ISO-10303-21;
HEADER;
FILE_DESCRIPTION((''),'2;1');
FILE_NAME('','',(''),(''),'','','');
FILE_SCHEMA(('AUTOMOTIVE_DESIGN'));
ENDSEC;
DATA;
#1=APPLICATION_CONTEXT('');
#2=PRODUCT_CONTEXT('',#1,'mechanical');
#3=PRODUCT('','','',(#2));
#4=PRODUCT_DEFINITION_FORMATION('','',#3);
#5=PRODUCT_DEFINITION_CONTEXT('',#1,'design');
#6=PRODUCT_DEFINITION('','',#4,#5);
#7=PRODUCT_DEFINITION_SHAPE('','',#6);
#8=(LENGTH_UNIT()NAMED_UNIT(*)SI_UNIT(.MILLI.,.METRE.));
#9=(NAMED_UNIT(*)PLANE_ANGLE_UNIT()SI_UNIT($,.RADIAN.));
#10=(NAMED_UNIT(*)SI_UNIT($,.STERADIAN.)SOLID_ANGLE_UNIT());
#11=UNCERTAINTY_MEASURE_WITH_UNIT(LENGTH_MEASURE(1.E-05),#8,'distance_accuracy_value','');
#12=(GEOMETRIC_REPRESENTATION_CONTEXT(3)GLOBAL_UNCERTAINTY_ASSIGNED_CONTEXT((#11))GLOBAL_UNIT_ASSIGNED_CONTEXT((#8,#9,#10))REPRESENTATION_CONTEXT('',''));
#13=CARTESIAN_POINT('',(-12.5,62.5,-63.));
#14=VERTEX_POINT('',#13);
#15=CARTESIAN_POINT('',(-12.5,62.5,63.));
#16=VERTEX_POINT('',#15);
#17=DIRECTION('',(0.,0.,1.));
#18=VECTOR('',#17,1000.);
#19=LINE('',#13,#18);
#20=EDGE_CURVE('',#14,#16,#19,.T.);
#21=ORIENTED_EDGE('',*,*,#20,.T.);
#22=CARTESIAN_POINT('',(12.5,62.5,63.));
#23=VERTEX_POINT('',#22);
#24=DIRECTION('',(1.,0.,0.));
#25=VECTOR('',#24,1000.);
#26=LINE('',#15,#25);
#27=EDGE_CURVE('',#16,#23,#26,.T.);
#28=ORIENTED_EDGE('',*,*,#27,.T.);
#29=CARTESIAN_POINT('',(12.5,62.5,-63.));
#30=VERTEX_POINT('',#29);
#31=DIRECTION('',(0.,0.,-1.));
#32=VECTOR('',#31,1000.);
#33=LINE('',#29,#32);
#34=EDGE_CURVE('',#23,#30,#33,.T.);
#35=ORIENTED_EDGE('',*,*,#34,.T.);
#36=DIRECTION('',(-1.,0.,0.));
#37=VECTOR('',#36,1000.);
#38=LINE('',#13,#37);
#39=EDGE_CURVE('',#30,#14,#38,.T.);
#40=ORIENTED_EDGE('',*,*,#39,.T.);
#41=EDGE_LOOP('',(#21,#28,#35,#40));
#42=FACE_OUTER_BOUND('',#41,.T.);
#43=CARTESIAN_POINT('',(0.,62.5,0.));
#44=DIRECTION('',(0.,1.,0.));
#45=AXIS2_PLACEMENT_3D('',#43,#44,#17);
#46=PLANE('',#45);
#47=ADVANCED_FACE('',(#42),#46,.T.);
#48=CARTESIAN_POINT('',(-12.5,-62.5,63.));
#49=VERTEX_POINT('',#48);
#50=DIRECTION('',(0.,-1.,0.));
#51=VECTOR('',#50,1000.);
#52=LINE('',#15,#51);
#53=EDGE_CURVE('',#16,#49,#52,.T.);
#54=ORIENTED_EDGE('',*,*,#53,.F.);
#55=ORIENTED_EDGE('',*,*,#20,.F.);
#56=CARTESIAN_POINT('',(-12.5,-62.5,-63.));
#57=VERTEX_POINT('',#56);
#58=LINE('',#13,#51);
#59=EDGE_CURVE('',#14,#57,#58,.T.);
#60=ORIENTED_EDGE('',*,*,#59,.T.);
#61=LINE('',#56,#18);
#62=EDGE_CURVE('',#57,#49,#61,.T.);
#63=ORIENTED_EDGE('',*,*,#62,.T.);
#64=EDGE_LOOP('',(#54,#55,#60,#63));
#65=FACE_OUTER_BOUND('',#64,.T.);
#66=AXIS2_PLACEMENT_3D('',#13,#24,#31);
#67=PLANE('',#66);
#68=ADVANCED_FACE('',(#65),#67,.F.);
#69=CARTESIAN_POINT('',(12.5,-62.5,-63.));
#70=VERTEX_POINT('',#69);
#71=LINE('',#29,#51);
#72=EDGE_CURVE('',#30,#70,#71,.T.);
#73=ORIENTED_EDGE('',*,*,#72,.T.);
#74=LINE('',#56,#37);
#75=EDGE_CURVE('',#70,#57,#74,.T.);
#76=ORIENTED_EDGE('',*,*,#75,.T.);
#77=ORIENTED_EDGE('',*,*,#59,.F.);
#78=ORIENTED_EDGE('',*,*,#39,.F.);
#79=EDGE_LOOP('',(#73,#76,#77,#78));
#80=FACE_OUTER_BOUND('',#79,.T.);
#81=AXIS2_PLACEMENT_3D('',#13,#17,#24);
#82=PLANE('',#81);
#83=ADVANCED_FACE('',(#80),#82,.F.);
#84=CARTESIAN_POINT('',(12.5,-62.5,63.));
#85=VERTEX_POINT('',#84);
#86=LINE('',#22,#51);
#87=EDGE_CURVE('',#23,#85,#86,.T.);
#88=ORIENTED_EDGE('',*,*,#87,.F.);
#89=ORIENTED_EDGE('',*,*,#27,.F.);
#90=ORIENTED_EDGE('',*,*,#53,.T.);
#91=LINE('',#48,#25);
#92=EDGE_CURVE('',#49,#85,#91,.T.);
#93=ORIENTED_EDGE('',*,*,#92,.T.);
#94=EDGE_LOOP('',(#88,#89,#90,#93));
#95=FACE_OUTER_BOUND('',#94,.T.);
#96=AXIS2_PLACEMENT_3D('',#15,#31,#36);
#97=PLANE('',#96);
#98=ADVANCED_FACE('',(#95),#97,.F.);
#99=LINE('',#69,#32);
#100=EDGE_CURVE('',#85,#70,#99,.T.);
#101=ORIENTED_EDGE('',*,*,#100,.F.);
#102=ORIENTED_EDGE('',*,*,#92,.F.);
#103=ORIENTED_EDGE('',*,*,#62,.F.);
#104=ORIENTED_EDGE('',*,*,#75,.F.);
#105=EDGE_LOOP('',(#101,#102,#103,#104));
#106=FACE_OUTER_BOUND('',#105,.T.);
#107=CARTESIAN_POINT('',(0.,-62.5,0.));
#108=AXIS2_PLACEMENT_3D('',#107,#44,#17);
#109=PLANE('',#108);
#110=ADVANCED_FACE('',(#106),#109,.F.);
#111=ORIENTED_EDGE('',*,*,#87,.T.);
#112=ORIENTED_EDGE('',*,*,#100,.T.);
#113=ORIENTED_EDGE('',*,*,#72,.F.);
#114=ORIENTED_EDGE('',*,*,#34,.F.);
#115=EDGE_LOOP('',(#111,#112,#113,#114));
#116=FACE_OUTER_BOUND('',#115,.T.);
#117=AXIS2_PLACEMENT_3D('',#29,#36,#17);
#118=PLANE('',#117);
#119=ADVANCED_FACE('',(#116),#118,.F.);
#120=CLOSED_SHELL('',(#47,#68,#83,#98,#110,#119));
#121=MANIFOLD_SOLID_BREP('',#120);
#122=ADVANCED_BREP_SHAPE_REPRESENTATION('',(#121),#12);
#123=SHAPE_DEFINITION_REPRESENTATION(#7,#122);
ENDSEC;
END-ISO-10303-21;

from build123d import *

# Parameters (mm, degrees)
SKETCH2_W           = 25
SKETCH2_H           = 126
BOSS_EXTRUDE1_DEPTH = 62.5


with BuildPart() as part:
    # Sketch2 → Boss-Extrude1 (new, symmetric)
    with BuildSketch(Plane(origin=(0, 0, 0), x_dir=(1, 0, 0), z_dir=(0, 1, 0))):
        Rectangle(SKETCH2_W, SKETCH2_H)
    extrude(amount=BOSS_EXTRUDE1_DEPTH, both=True)


solid = part.part
